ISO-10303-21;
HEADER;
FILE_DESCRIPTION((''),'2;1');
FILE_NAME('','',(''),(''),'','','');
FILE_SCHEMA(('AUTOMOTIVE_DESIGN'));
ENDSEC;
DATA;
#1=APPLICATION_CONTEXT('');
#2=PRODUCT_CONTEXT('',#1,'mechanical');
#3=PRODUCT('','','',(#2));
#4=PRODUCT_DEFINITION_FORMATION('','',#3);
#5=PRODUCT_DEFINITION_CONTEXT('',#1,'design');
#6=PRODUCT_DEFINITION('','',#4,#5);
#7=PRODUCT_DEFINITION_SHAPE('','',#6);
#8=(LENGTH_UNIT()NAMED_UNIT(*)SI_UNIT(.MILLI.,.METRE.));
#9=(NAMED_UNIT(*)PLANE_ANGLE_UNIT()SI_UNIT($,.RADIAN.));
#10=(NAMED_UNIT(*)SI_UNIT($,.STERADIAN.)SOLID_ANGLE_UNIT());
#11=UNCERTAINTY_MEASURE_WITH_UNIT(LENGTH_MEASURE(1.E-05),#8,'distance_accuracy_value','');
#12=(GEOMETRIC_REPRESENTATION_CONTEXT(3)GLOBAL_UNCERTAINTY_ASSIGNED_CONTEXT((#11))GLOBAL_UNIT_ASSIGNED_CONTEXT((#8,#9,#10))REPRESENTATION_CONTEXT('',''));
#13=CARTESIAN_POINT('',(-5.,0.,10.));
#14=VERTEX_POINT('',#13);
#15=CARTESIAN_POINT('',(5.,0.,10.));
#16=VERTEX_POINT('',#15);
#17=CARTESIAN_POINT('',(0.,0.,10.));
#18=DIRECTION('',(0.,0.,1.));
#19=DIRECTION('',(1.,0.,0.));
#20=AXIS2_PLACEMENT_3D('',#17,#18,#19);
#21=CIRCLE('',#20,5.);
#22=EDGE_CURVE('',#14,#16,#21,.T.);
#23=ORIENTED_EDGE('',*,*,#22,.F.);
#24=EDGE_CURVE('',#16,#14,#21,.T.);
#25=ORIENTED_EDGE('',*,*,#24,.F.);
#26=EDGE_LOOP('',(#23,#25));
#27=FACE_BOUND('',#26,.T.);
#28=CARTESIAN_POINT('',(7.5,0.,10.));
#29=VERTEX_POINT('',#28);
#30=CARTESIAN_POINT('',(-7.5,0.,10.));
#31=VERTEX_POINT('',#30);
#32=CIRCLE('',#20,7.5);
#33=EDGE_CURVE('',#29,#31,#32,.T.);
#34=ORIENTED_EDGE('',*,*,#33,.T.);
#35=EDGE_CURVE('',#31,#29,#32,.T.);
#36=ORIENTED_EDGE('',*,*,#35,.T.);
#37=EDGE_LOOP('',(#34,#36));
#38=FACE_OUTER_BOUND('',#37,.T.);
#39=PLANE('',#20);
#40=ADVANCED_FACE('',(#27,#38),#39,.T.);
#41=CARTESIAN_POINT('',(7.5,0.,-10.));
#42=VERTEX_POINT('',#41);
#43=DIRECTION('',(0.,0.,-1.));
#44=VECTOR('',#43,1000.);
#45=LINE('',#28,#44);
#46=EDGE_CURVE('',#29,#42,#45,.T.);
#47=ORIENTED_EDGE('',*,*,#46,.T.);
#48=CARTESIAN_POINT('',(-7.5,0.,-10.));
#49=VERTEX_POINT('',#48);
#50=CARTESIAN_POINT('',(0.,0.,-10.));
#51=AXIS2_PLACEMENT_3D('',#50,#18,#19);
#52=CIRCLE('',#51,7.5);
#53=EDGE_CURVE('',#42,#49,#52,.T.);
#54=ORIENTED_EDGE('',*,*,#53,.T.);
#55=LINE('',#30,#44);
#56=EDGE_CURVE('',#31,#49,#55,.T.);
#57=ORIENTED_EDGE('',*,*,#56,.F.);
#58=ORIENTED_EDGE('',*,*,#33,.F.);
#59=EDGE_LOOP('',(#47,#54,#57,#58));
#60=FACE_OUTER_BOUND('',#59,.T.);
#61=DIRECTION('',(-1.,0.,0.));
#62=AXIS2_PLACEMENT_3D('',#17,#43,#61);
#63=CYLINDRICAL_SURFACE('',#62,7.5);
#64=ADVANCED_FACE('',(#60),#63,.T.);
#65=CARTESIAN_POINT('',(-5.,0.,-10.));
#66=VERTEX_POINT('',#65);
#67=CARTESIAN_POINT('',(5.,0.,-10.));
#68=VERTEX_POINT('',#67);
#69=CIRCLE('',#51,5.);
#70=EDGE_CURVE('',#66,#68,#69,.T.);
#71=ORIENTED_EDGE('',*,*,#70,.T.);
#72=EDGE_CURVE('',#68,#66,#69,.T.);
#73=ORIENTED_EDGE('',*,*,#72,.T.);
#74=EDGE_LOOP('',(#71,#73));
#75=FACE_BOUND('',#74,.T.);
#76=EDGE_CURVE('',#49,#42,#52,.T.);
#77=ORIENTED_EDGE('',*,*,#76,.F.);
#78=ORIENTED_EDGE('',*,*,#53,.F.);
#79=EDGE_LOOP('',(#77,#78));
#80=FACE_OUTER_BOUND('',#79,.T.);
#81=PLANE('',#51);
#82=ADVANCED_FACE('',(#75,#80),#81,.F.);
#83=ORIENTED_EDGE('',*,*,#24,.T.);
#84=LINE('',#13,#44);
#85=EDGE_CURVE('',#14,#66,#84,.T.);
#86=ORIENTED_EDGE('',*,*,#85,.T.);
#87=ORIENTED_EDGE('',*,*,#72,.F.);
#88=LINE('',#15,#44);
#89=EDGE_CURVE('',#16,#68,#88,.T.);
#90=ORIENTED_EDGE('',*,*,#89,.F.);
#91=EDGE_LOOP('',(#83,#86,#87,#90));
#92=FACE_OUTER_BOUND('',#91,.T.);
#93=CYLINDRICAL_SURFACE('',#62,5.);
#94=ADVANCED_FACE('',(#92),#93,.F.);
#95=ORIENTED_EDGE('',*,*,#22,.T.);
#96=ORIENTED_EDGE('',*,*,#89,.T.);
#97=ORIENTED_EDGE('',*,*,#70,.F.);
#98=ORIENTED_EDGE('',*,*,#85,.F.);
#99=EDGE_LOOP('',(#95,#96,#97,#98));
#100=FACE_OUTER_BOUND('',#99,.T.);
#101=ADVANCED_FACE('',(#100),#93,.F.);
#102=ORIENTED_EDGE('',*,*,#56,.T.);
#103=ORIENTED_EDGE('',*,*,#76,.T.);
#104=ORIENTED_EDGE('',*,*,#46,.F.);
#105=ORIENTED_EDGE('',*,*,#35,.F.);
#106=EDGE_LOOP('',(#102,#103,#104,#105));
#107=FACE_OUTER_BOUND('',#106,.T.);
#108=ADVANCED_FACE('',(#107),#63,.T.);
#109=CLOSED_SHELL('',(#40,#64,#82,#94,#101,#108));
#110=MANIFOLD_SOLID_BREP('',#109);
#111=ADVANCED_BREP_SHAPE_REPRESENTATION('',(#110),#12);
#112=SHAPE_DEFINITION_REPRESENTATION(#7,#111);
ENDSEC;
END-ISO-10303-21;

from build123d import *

# Parameters (mm, degrees)
SKETCH2_R           = 7.5
SKETCH2_R_2         = 5
BOSS_EXTRUDE1_DEPTH = 10


with BuildPart() as part:
    # Sketch2 → Boss-Extrude1 (new, symmetric)
    with BuildSketch(Plane.XY):
        Circle(SKETCH2_R)
        Circle(SKETCH2_R_2, mode=Mode.SUBTRACT)
    extrude(amount=BOSS_EXTRUDE1_DEPTH, both=True)


solid = part.part
